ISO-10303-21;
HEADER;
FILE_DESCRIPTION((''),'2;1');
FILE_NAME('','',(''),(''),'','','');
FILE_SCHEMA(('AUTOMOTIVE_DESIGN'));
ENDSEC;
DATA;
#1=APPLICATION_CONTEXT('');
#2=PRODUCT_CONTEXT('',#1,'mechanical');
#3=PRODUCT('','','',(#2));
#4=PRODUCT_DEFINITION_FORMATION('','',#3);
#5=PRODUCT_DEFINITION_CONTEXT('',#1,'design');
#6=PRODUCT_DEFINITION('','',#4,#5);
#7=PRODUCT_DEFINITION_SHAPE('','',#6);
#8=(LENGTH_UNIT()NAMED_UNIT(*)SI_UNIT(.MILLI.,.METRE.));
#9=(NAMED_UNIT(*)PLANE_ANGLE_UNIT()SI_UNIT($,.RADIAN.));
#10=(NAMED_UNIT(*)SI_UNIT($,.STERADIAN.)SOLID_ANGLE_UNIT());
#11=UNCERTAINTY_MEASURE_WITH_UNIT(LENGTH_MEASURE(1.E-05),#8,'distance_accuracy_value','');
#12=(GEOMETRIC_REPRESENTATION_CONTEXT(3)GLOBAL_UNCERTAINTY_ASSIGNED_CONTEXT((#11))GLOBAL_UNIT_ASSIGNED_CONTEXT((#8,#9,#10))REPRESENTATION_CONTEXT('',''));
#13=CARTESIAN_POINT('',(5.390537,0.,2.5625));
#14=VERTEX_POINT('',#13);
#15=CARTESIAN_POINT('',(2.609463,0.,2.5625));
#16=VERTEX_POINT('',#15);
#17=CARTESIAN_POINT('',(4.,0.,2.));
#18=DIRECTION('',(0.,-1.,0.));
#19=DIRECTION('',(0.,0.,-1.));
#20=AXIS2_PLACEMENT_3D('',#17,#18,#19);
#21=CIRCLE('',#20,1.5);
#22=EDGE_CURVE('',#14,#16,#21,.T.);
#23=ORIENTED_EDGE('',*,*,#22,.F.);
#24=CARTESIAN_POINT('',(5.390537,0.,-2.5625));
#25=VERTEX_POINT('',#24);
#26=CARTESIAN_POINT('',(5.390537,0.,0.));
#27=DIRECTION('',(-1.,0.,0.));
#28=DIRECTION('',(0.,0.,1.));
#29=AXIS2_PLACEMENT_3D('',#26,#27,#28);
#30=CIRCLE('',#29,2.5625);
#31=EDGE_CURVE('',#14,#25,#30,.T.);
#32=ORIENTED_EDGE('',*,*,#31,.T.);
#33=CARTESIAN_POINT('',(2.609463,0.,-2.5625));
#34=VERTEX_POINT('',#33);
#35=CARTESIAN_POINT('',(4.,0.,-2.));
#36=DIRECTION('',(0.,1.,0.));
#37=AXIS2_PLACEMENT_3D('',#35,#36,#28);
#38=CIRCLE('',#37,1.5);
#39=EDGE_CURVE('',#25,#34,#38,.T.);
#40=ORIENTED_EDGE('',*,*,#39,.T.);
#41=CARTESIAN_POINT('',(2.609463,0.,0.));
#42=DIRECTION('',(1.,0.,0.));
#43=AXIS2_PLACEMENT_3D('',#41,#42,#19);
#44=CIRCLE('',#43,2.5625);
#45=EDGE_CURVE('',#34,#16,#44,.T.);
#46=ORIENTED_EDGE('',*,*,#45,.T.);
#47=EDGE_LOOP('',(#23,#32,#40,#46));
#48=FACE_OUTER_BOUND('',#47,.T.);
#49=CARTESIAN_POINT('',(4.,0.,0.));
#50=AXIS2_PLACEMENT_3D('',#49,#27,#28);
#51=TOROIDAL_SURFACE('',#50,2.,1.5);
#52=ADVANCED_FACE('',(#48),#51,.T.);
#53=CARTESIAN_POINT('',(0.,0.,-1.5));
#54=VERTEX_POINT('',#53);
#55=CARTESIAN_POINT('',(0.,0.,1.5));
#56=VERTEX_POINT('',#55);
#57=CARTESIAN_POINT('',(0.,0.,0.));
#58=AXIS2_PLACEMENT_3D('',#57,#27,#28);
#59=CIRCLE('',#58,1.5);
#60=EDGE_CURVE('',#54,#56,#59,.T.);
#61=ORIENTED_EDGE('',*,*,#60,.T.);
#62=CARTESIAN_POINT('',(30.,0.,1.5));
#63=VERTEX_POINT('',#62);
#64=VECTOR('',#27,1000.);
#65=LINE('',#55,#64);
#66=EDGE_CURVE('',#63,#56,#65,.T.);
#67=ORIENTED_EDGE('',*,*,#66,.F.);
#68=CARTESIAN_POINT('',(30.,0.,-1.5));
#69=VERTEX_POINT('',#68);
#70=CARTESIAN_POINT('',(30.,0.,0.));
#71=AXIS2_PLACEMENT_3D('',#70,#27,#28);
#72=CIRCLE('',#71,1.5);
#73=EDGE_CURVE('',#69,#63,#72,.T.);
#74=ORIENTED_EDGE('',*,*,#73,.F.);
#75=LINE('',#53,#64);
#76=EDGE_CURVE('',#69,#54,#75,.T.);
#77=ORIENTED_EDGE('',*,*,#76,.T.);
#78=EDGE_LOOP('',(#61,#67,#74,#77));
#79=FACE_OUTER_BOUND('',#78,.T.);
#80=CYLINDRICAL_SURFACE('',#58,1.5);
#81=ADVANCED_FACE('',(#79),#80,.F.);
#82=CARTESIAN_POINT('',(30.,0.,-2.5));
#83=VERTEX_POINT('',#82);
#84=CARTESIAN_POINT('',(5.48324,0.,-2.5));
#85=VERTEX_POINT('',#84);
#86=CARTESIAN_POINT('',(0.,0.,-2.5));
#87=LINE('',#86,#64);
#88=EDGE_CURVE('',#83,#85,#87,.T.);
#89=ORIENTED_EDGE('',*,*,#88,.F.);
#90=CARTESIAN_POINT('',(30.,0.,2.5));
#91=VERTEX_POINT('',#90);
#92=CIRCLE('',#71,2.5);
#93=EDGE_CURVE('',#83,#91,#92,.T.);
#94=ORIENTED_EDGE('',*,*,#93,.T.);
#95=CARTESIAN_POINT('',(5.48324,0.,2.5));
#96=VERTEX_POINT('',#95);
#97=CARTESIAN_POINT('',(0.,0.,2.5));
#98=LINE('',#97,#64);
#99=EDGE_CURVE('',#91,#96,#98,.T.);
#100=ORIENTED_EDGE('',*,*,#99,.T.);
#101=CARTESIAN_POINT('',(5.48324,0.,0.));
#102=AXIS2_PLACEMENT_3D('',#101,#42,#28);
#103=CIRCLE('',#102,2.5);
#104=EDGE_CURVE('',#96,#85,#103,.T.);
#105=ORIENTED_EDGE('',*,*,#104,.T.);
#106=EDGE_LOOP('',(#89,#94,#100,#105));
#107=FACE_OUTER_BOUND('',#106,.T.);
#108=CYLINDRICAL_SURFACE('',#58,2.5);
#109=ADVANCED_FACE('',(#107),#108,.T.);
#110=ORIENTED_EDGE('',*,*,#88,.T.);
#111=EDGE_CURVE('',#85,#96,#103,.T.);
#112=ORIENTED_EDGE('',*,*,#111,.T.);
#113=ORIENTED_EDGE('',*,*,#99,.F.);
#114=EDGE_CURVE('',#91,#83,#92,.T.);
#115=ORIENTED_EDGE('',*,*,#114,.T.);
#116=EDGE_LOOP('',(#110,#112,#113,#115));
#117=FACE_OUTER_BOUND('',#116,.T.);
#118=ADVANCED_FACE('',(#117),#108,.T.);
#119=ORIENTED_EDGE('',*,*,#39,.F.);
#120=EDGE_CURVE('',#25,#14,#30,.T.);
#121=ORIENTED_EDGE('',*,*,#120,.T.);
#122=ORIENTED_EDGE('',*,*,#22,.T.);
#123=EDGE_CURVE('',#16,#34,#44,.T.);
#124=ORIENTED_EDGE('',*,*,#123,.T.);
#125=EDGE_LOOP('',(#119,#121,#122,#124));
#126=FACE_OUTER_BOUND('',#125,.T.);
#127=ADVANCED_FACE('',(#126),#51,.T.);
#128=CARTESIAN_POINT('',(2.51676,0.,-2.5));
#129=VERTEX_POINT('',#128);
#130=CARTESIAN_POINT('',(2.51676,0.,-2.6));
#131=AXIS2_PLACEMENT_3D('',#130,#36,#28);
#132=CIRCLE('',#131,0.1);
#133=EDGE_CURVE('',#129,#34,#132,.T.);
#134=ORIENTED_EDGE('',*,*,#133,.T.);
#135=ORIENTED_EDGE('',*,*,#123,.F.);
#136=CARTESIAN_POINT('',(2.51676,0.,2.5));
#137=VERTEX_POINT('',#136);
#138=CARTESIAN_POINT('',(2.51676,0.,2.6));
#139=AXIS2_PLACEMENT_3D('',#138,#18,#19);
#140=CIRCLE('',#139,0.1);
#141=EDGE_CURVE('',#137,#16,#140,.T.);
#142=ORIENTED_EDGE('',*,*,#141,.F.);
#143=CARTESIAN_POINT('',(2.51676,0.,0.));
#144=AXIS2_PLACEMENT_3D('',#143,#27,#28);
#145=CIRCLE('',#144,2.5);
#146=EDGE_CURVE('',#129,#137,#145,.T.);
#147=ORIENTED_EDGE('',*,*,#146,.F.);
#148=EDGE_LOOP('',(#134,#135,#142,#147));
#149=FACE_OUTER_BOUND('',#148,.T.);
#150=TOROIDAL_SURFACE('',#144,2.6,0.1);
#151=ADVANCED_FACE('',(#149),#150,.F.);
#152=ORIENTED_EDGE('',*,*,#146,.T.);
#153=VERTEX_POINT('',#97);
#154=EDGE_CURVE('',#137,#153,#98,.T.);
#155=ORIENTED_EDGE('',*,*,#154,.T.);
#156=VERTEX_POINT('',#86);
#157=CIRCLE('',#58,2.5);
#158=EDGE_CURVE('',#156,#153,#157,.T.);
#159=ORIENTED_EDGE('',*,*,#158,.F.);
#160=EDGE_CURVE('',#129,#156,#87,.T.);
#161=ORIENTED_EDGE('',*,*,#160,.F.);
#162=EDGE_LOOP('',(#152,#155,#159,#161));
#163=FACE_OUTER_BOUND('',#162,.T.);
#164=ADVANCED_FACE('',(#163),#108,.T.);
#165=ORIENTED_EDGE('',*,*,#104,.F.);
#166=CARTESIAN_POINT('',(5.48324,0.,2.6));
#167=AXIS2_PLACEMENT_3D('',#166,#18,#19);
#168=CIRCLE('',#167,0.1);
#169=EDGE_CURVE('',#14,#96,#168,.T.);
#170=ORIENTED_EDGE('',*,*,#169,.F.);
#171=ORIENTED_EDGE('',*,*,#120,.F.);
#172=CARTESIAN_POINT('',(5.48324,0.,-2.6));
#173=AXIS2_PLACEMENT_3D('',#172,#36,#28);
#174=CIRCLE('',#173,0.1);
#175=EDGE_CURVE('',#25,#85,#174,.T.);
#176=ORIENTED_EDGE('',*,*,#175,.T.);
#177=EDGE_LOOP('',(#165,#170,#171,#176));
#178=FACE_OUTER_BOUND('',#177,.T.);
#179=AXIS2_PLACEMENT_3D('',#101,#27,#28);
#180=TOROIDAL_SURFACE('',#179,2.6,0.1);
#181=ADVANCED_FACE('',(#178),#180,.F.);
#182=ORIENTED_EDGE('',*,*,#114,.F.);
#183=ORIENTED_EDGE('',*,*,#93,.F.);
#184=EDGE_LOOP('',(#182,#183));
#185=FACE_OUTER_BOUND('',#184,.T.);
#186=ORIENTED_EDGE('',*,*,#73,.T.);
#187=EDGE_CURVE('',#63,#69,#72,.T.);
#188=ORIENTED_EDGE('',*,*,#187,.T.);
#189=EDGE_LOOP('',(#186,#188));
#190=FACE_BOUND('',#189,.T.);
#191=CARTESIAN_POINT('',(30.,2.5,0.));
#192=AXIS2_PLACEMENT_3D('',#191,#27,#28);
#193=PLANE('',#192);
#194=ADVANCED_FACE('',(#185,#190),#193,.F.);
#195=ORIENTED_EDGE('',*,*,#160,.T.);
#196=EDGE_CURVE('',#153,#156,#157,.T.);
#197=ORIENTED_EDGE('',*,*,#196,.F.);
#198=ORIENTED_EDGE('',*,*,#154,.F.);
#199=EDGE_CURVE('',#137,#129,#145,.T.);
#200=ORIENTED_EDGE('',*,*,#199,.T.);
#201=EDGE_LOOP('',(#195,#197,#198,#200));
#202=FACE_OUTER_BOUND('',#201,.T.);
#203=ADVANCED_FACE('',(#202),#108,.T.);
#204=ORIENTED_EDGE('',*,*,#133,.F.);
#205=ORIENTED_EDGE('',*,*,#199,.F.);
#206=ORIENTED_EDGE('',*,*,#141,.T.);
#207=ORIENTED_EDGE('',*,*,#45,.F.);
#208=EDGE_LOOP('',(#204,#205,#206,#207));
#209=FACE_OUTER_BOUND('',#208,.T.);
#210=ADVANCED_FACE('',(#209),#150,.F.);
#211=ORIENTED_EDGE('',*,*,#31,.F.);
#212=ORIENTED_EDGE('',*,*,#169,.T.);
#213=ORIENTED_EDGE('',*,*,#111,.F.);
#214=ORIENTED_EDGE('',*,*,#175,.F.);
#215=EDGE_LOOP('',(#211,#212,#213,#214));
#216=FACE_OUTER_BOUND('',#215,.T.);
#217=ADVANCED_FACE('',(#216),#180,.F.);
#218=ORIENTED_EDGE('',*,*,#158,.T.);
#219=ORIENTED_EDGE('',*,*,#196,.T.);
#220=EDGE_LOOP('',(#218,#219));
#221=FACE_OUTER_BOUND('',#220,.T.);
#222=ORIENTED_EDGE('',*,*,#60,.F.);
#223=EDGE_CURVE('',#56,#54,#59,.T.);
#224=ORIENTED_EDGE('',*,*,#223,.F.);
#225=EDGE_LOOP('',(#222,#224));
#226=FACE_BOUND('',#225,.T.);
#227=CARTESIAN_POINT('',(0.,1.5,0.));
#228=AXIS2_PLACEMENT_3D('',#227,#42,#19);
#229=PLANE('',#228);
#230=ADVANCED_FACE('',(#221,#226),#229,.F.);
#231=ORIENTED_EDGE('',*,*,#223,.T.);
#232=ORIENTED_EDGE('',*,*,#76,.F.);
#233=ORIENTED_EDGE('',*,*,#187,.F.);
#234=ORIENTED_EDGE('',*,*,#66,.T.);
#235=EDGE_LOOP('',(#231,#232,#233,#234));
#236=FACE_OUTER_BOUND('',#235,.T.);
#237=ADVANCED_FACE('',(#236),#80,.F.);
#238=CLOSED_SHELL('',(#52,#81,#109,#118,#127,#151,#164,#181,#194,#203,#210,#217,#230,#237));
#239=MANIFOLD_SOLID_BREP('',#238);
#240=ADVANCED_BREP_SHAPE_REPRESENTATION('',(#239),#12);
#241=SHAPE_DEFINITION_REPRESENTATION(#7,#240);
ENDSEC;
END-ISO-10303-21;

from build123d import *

# Parameters (mm, degrees)
FILLET1_R = 0.1


with BuildPart() as part:
    # Sketch1 → Revolve1 (revolve)
    with BuildSketch(Plane.XY, mode=Mode.PRIVATE) as revolve1_sk:
        with BuildLine():
            Line((0, 2.5), (2.585786438, 2.5))
            ThreePointArc((2.585786438, 2.5), (4, 3.5), (5.414213562, 2.5))
            Line((5.414213562, 2.5), (30, 2.5))
            Line((30, 2.5), (30, 1.5))
            Line((30, 1.5), (0, 1.5))
            Line((0, 1.5), (0, 2.5))
        make_face()
    revolve(revolve1_sk.sketch.rotate(Axis((0, 0, 0), (1, 0, 0)), 90), axis=Axis((0, 0, 0), (1, 0, 0)))

    # Fillet1
    fillet1_edges = [part.edges().sort_by_distance(p)[0] for p in [
        (2.585786438, 0, -2.5),
        (5.414213562, 0, -2.5),
    ]]
    fillet(fillet1_edges, radius=FILLET1_R)


solid = part.part
